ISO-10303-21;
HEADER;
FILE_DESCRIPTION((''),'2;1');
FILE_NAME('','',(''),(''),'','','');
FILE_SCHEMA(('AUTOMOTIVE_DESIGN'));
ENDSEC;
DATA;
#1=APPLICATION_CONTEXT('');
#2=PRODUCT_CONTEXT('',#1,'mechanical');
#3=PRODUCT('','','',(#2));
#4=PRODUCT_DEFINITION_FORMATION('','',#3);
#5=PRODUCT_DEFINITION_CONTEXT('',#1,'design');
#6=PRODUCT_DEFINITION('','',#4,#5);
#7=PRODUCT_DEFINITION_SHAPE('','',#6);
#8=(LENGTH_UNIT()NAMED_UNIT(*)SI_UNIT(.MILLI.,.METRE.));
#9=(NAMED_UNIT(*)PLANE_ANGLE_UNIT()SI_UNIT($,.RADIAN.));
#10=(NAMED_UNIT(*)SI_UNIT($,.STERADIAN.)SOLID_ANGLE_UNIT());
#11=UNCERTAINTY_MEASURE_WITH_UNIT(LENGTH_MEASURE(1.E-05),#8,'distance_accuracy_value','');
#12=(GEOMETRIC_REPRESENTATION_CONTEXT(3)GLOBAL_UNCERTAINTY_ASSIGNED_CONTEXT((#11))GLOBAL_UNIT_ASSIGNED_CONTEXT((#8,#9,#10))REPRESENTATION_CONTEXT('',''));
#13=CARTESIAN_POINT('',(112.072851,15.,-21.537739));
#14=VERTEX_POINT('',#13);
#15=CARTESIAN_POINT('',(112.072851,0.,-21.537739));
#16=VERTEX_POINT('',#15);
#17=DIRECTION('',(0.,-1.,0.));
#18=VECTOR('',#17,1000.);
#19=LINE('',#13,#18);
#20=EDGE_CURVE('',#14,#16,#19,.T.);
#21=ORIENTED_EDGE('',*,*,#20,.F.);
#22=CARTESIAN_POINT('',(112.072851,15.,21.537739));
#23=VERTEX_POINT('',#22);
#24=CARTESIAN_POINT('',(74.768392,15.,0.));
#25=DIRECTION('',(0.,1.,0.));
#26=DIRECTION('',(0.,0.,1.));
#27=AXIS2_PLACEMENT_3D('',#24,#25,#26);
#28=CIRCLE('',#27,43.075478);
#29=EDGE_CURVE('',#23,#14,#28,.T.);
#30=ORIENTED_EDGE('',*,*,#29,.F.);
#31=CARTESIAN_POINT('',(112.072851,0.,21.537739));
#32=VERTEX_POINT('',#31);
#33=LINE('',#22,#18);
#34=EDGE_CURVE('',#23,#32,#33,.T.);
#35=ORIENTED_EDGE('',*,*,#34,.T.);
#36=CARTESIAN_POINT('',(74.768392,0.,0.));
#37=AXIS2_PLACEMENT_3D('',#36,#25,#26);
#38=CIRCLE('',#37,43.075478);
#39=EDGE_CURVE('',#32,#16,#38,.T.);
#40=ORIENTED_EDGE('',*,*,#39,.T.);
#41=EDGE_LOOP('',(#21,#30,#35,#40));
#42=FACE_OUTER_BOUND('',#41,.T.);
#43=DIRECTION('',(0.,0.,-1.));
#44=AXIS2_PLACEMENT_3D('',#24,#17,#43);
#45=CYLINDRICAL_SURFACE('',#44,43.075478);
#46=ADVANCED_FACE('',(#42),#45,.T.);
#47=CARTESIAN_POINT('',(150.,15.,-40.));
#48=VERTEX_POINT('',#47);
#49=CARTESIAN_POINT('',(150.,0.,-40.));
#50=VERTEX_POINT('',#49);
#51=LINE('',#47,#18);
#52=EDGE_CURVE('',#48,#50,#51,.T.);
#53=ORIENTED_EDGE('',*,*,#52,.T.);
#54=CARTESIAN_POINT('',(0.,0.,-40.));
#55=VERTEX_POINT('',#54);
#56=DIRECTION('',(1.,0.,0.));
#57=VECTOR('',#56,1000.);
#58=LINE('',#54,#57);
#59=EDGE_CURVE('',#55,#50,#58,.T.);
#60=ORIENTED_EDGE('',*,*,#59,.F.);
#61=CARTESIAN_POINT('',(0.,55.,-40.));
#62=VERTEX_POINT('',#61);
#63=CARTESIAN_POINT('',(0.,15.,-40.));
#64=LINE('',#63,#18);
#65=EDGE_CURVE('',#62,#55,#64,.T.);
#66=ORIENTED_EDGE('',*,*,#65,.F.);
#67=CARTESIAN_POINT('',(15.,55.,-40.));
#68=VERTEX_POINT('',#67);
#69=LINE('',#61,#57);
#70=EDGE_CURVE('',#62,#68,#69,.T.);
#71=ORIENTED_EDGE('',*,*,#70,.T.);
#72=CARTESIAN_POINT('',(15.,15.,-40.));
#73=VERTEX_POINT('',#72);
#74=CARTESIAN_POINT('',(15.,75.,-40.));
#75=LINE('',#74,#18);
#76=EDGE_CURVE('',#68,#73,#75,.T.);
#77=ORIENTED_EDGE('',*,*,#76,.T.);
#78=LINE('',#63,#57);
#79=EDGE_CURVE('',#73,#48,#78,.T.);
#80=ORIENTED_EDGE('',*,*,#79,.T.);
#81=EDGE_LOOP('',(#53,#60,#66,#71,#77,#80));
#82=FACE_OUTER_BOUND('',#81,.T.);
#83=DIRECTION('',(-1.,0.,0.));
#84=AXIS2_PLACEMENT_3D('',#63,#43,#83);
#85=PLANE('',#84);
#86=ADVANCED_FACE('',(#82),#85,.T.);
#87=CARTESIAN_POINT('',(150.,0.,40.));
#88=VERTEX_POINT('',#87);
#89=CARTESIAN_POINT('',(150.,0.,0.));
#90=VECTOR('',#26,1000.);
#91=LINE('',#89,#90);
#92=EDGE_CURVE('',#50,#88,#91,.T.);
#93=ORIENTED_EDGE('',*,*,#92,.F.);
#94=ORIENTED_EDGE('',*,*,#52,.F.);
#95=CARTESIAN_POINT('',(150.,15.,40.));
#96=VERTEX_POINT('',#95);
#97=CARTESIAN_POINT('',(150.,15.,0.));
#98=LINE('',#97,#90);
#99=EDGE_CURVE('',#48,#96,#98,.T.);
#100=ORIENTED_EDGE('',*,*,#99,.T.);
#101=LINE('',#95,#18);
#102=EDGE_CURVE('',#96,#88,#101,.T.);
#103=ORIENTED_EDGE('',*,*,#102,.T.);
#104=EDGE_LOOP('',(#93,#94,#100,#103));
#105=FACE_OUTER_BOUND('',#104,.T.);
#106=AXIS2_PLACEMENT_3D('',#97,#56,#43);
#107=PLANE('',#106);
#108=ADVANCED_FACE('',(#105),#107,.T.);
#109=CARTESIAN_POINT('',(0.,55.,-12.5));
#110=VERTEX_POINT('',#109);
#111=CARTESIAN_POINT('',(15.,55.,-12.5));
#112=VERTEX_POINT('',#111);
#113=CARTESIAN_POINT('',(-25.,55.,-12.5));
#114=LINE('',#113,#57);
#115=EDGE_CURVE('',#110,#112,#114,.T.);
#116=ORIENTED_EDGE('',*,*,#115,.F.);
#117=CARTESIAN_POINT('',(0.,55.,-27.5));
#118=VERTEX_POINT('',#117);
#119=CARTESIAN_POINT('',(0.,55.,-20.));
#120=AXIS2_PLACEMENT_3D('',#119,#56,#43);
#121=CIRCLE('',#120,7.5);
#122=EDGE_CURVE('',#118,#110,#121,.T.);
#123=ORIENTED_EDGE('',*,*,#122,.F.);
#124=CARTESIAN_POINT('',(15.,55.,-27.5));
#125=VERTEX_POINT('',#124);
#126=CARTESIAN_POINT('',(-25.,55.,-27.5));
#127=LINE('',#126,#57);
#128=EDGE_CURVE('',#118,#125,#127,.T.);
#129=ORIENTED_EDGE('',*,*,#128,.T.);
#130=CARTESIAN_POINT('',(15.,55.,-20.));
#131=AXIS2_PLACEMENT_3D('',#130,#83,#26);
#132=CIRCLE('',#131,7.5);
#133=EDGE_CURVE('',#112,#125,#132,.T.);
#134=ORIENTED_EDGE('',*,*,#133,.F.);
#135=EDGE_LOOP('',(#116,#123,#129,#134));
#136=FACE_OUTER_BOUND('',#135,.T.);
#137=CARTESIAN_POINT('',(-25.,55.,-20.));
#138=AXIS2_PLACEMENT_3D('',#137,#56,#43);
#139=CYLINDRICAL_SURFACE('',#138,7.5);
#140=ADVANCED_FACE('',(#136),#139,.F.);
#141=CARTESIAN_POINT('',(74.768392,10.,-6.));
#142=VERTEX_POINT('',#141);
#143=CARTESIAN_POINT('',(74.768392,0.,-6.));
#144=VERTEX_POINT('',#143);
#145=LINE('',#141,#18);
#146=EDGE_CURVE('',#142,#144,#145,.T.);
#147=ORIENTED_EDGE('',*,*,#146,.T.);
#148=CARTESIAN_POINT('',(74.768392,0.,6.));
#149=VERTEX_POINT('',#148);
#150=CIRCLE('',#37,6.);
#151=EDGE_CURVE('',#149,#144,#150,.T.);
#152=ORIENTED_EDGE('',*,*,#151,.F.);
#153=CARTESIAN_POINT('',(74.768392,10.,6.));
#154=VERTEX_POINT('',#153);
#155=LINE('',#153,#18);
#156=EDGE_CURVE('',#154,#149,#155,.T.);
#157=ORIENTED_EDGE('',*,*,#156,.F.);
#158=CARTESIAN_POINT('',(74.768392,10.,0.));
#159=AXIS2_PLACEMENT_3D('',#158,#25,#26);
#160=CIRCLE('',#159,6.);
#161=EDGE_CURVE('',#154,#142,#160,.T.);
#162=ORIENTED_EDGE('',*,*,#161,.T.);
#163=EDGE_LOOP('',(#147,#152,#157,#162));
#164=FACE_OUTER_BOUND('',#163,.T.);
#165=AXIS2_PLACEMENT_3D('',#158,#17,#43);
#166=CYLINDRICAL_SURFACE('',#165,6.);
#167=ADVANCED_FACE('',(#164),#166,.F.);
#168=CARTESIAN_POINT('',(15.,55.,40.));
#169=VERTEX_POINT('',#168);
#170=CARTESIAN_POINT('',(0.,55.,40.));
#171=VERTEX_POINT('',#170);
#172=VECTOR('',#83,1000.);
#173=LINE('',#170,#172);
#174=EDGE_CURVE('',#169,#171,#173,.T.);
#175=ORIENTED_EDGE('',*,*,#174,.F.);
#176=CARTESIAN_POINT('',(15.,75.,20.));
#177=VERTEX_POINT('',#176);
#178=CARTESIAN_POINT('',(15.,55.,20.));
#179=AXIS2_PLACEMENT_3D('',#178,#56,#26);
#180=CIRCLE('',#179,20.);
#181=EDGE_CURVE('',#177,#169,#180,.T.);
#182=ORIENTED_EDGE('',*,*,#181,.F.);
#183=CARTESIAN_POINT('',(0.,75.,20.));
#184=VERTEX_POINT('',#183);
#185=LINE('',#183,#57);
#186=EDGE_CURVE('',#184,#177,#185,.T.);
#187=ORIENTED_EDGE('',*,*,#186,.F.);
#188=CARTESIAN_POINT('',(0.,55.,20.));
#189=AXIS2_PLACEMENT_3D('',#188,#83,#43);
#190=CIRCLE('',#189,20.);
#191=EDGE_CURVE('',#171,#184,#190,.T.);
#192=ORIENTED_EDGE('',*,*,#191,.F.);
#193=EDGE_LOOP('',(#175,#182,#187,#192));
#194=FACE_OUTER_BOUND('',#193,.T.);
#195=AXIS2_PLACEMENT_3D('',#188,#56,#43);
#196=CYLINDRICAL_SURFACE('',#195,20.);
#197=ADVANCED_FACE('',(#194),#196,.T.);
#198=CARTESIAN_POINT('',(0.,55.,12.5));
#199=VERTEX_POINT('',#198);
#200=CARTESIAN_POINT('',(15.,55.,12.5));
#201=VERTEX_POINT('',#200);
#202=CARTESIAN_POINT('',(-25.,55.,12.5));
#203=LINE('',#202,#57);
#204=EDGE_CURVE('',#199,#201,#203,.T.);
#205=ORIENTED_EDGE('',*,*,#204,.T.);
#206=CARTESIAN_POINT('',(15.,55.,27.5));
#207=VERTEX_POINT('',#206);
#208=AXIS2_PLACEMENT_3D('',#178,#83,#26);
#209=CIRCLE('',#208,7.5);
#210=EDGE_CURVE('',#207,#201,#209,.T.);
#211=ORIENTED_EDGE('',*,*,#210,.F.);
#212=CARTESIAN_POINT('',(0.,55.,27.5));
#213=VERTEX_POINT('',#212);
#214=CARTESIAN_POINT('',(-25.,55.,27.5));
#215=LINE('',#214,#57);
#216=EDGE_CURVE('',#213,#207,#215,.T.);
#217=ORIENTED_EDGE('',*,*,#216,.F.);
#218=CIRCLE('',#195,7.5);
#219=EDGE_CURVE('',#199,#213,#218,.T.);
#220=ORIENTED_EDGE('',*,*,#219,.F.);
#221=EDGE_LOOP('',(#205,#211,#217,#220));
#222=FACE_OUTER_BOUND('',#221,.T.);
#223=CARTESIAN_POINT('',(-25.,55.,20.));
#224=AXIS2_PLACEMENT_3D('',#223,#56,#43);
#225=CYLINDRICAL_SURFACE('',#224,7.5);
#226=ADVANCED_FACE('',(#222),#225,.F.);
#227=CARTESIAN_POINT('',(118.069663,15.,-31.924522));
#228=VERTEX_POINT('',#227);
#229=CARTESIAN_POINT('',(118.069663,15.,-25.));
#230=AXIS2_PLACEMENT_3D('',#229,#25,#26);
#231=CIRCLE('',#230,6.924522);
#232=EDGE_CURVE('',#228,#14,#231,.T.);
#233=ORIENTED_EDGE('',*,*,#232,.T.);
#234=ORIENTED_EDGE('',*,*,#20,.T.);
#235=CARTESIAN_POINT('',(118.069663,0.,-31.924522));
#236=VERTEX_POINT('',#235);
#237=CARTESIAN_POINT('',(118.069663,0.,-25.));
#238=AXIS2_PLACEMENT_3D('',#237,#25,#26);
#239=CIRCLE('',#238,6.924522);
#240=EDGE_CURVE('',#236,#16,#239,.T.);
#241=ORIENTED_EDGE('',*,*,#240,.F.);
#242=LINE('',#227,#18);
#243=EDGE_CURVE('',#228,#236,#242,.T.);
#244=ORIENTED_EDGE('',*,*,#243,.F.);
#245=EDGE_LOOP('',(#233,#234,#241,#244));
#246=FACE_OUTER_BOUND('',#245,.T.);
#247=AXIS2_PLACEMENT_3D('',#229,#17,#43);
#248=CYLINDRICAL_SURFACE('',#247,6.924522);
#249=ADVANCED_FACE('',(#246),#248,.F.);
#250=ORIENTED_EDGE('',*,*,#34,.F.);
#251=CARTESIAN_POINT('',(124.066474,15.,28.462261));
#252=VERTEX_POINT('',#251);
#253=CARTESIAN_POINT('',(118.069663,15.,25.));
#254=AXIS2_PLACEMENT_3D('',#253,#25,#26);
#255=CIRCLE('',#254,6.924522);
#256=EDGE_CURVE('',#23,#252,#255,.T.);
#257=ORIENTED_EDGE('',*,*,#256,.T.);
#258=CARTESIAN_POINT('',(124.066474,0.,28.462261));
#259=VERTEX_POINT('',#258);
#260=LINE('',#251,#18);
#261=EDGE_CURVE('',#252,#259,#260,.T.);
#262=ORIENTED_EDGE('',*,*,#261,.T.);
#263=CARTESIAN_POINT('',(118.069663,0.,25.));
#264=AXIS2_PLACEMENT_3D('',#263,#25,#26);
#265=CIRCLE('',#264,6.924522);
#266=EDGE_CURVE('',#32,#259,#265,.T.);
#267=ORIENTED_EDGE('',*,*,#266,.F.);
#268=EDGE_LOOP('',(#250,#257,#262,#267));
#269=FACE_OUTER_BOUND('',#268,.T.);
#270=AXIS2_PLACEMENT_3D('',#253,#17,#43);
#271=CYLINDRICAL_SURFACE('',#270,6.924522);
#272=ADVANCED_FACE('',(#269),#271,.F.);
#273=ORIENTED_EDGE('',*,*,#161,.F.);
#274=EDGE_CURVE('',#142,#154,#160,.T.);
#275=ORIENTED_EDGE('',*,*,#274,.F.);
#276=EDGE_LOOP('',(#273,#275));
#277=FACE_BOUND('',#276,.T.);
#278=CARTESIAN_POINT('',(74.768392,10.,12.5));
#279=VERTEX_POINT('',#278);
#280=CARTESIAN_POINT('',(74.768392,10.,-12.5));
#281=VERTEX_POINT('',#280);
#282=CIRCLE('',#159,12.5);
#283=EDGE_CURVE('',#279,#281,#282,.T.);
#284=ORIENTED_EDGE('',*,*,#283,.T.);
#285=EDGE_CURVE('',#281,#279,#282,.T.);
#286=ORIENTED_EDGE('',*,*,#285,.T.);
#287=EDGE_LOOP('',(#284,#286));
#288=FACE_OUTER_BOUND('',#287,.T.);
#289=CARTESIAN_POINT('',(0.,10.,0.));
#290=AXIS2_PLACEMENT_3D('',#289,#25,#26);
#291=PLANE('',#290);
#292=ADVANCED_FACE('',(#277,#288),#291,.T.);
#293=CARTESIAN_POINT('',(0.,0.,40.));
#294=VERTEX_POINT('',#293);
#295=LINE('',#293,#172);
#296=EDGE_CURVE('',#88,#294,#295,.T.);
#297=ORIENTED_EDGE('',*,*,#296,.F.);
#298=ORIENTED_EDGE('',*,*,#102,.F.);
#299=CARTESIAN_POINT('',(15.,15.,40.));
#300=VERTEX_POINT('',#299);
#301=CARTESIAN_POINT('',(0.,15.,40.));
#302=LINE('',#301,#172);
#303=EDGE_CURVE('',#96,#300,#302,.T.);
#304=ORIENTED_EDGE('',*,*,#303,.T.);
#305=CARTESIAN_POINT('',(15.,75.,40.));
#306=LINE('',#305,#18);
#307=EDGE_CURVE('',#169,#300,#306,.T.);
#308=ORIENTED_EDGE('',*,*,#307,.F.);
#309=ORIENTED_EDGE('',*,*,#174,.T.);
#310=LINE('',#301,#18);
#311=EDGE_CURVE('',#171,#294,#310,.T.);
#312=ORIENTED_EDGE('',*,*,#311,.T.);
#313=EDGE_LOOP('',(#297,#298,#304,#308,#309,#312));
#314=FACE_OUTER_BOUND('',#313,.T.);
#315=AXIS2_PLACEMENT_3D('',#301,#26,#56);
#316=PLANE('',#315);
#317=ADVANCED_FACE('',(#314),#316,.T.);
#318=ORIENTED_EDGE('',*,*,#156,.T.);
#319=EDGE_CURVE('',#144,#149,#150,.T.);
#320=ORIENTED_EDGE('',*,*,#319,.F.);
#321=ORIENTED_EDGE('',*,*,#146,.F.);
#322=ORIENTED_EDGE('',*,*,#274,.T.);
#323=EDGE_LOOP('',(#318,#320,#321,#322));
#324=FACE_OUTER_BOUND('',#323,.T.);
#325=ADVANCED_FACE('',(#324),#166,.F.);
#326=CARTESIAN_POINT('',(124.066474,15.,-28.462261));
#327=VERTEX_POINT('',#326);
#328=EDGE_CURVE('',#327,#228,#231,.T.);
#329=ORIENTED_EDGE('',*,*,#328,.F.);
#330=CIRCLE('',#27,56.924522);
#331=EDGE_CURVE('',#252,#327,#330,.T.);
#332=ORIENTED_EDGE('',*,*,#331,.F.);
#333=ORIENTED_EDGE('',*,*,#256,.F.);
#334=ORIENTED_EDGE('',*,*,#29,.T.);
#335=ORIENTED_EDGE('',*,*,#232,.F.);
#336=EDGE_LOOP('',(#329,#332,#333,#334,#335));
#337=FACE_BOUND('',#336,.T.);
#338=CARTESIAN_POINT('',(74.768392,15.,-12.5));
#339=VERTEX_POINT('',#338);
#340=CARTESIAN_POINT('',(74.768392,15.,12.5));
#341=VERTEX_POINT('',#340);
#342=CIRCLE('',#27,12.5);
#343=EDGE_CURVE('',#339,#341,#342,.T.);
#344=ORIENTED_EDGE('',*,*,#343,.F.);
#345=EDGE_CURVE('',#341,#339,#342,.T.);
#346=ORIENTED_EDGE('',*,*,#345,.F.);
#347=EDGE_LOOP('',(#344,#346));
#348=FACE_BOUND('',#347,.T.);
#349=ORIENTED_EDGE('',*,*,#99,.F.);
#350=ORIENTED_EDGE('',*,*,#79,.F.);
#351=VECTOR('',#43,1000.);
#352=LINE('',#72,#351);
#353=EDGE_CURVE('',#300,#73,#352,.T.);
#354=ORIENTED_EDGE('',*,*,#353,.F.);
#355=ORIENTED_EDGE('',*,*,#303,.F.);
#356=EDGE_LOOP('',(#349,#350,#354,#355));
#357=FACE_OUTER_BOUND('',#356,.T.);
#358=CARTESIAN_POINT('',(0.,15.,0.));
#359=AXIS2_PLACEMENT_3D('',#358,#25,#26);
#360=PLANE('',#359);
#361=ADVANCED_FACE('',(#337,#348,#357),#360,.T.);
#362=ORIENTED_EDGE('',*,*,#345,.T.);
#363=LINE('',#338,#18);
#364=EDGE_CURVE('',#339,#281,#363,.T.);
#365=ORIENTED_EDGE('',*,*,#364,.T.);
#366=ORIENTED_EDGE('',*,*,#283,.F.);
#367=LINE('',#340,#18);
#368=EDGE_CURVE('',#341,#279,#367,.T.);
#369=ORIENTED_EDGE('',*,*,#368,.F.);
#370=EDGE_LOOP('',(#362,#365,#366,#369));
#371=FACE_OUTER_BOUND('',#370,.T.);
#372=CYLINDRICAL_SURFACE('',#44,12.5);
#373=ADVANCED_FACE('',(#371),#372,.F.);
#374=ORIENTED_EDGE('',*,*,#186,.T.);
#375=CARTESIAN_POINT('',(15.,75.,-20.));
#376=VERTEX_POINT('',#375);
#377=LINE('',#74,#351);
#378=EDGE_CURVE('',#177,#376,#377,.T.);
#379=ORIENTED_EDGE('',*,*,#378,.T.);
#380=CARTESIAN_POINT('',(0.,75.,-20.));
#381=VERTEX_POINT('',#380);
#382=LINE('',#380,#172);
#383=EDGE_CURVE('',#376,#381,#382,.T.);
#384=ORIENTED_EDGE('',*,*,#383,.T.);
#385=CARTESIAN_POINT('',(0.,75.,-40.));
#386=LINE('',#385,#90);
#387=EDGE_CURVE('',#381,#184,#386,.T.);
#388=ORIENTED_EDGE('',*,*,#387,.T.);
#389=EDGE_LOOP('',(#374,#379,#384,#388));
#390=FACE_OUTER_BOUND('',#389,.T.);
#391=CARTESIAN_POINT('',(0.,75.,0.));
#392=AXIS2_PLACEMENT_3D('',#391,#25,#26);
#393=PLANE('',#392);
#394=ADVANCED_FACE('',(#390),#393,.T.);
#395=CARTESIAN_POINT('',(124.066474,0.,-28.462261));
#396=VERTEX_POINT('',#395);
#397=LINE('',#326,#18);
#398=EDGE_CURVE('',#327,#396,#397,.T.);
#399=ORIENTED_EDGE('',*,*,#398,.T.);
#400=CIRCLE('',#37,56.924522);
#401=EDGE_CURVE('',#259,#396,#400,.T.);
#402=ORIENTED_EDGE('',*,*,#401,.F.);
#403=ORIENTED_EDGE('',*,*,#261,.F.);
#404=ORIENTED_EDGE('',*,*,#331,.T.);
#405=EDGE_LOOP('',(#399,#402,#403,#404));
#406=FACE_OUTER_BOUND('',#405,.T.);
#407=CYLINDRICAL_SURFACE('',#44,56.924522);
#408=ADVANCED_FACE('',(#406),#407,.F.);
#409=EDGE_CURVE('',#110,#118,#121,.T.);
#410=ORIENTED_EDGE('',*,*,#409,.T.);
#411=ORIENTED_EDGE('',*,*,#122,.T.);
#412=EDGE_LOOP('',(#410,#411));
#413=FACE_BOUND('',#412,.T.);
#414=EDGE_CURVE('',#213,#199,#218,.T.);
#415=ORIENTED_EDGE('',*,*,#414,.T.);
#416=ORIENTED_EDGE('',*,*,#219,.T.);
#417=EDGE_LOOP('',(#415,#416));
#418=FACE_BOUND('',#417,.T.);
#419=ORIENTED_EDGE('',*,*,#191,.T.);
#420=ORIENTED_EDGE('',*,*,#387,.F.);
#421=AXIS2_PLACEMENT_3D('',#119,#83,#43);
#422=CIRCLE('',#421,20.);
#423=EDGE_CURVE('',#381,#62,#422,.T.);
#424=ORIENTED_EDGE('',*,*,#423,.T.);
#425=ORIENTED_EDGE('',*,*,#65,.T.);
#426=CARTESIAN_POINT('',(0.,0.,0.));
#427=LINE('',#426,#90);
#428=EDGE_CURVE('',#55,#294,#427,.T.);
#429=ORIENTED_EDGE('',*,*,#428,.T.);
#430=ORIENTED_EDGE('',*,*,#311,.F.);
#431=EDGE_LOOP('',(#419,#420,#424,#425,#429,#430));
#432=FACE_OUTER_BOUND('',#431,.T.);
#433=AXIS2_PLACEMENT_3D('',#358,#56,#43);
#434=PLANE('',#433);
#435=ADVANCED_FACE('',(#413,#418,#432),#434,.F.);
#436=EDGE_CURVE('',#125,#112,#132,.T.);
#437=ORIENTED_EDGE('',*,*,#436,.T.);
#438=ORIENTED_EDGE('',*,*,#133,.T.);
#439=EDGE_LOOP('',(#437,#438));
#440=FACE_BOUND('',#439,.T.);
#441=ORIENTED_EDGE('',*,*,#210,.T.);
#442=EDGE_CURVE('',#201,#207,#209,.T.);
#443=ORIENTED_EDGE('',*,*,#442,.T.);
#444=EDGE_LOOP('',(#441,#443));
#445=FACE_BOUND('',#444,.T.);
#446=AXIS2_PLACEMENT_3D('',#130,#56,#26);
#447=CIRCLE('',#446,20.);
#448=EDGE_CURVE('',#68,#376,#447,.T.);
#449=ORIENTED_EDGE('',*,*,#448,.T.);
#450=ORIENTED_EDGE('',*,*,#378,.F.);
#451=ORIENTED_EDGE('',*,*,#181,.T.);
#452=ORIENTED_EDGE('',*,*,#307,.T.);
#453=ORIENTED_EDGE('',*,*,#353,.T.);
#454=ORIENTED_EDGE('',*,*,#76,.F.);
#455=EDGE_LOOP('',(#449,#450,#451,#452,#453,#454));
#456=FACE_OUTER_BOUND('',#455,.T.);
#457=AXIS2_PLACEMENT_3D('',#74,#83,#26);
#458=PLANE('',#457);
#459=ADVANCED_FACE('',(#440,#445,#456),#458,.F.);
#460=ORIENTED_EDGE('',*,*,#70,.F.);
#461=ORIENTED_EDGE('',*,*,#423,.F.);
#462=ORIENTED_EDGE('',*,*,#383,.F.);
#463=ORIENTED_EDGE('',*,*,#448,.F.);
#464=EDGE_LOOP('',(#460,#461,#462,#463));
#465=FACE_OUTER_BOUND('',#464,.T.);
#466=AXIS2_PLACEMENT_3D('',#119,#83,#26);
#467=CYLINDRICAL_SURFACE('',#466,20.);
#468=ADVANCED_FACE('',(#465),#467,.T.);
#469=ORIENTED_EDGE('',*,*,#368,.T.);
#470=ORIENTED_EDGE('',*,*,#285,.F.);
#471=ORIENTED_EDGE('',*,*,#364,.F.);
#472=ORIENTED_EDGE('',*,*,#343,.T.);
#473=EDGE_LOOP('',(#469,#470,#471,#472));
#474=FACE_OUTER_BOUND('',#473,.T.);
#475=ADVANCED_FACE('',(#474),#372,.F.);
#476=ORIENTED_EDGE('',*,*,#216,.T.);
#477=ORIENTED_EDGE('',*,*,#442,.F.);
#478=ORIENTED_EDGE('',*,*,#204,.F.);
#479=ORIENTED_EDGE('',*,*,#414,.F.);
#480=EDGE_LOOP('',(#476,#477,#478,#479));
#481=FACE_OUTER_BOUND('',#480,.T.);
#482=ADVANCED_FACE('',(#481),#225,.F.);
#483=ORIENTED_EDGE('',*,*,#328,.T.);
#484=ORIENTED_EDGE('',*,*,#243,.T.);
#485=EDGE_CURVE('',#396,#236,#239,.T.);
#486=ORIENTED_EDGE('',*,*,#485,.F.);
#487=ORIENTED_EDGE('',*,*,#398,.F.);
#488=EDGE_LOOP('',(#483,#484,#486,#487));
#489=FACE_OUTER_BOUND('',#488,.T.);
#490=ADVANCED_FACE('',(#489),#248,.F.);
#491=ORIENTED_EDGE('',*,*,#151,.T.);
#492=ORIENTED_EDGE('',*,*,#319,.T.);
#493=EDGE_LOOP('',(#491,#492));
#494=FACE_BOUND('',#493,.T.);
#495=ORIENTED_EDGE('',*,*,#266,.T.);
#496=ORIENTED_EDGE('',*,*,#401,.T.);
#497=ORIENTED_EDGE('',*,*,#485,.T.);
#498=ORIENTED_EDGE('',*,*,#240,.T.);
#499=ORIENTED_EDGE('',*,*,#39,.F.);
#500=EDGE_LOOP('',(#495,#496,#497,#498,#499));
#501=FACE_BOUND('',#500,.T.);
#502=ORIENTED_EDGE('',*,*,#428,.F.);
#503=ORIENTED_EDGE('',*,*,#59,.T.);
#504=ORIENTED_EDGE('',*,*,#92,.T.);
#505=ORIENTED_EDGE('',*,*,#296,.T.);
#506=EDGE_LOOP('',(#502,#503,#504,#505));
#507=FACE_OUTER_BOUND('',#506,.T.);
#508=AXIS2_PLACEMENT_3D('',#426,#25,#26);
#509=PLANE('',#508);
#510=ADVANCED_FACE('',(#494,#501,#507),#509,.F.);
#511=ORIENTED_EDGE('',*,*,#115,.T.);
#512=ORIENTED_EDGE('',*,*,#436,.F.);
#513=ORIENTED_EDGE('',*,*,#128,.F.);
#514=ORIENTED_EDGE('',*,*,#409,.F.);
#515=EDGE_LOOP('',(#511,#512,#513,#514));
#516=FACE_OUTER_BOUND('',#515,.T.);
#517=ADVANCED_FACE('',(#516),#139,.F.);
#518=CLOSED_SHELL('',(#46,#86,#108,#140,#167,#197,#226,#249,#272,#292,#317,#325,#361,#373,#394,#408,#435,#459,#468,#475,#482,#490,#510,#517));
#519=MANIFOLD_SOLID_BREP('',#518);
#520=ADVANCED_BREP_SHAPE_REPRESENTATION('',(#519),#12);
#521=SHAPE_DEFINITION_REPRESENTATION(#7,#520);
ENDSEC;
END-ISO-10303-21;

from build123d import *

# Parameters (mm, degrees)
BASE_PLATE_SKETCH_W             = 150
BASE_PLATE_SKETCH_H             = 80
BASE_PLATE_SKETCH_R             = 12.5
BASE_PLATE_DEPTH                = 15
SKETCH1_4_R                     = 12.5
SKETCH1_4_R_2                   = 6
BASE_CONTOUR_EXTRUDE_10MM_DEPTH = 10
UPRIGHT_WALL_SKETCH_W           = 15
UPRIGHT_WALL_SKETCH_H           = 80
UPRIGHT_WALL_DEPTH              = 60
UPRIGHT_TOP_FILLET_R20_R        = 20
UPRIGHT_HOLES_SKETCH_R          = 7.5
UPRIGHT_MOUNTING_HOLES_DEPTH    = 40


with BuildPart() as part:
    # Base Plate Sketch → Base Plate (new body)
    with BuildSketch(Plane(origin=(0, 0, 0), x_dir=(1, 0, 0), z_dir=(0, 1, 0))):
        with Locations((75, 0)):
            Rectangle(BASE_PLATE_SKETCH_W, BASE_PLATE_SKETCH_H)
        with Locations(Location((74.768392371, 0, 0), (0, 0, 270))):
            Circle(BASE_PLATE_SKETCH_R, mode=Mode.SUBTRACT)
        with BuildLine():
            ThreePointArc((124.066474122, 28.46226077), (114.60740179, 30.996811562), (112.072850998, 21.53773923))
            ThreePointArc((112.072850998, 21.53773923), (117.843870831, 0), (112.072850998, -21.53773923))
            ThreePointArc((112.072850998, -21.53773923), (114.60740179, -30.996811562), (124.066474122, -28.46226077))
            ThreePointArc((124.066474122, -28.46226077), (131.69291391, 0), (124.066474122, 28.46226077))
        make_face(mode=Mode.SUBTRACT)
    extrude(amount=BASE_PLATE_DEPTH)

    # Sketch1_4 → Base Contour Extrude 10mm (add)
    with BuildSketch(Plane(origin=(0, 0, 0), x_dir=(1, 0, 0), z_dir=(0, 1, 0))):
        with Locations(Location((74.768392371, 0, 0), (0, 0, 270))):
            Circle(SKETCH1_4_R)
        with Locations(Location((74.768392371, 0, 0), (0, 0, 270))):
            Circle(SKETCH1_4_R_2, mode=Mode.SUBTRACT)
    extrude(amount=BASE_CONTOUR_EXTRUDE_10MM_DEPTH)

    # Upright Wall Sketch → Upright Wall (add)
    with BuildSketch(Plane(origin=(0, 15, 0), x_dir=(1, 0, 0), z_dir=(0, 1, 0))):
        with Locations((7.5, 0)):
            Rectangle(UPRIGHT_WALL_SKETCH_W, UPRIGHT_WALL_SKETCH_H)
    extrude(amount=UPRIGHT_WALL_DEPTH)

    # Upright Top Fillet R20
    upright_top_fillet_r20_edges = [part.edges().sort_by_distance(p)[0] for p in [
        (7.5, 75, 40),
        (7.5, 75, -40),
    ]]
    fillet(upright_top_fillet_r20_edges, radius=UPRIGHT_TOP_FILLET_R20_R)

    # Upright Holes Sketch → Upright Mounting Holes (cut, symmetric)
    with BuildSketch(Plane(origin=(15, 0, 0), x_dir=(0, 0, -1), z_dir=(1, 0, 0))):
        with Locations((20, 55)):
            Circle(UPRIGHT_HOLES_SKETCH_R)
        with Locations((-20, 55)):
            Circle(UPRIGHT_HOLES_SKETCH_R)
    extrude(amount=UPRIGHT_MOUNTING_HOLES_DEPTH, both=True, mode=Mode.SUBTRACT)


solid = part.part
